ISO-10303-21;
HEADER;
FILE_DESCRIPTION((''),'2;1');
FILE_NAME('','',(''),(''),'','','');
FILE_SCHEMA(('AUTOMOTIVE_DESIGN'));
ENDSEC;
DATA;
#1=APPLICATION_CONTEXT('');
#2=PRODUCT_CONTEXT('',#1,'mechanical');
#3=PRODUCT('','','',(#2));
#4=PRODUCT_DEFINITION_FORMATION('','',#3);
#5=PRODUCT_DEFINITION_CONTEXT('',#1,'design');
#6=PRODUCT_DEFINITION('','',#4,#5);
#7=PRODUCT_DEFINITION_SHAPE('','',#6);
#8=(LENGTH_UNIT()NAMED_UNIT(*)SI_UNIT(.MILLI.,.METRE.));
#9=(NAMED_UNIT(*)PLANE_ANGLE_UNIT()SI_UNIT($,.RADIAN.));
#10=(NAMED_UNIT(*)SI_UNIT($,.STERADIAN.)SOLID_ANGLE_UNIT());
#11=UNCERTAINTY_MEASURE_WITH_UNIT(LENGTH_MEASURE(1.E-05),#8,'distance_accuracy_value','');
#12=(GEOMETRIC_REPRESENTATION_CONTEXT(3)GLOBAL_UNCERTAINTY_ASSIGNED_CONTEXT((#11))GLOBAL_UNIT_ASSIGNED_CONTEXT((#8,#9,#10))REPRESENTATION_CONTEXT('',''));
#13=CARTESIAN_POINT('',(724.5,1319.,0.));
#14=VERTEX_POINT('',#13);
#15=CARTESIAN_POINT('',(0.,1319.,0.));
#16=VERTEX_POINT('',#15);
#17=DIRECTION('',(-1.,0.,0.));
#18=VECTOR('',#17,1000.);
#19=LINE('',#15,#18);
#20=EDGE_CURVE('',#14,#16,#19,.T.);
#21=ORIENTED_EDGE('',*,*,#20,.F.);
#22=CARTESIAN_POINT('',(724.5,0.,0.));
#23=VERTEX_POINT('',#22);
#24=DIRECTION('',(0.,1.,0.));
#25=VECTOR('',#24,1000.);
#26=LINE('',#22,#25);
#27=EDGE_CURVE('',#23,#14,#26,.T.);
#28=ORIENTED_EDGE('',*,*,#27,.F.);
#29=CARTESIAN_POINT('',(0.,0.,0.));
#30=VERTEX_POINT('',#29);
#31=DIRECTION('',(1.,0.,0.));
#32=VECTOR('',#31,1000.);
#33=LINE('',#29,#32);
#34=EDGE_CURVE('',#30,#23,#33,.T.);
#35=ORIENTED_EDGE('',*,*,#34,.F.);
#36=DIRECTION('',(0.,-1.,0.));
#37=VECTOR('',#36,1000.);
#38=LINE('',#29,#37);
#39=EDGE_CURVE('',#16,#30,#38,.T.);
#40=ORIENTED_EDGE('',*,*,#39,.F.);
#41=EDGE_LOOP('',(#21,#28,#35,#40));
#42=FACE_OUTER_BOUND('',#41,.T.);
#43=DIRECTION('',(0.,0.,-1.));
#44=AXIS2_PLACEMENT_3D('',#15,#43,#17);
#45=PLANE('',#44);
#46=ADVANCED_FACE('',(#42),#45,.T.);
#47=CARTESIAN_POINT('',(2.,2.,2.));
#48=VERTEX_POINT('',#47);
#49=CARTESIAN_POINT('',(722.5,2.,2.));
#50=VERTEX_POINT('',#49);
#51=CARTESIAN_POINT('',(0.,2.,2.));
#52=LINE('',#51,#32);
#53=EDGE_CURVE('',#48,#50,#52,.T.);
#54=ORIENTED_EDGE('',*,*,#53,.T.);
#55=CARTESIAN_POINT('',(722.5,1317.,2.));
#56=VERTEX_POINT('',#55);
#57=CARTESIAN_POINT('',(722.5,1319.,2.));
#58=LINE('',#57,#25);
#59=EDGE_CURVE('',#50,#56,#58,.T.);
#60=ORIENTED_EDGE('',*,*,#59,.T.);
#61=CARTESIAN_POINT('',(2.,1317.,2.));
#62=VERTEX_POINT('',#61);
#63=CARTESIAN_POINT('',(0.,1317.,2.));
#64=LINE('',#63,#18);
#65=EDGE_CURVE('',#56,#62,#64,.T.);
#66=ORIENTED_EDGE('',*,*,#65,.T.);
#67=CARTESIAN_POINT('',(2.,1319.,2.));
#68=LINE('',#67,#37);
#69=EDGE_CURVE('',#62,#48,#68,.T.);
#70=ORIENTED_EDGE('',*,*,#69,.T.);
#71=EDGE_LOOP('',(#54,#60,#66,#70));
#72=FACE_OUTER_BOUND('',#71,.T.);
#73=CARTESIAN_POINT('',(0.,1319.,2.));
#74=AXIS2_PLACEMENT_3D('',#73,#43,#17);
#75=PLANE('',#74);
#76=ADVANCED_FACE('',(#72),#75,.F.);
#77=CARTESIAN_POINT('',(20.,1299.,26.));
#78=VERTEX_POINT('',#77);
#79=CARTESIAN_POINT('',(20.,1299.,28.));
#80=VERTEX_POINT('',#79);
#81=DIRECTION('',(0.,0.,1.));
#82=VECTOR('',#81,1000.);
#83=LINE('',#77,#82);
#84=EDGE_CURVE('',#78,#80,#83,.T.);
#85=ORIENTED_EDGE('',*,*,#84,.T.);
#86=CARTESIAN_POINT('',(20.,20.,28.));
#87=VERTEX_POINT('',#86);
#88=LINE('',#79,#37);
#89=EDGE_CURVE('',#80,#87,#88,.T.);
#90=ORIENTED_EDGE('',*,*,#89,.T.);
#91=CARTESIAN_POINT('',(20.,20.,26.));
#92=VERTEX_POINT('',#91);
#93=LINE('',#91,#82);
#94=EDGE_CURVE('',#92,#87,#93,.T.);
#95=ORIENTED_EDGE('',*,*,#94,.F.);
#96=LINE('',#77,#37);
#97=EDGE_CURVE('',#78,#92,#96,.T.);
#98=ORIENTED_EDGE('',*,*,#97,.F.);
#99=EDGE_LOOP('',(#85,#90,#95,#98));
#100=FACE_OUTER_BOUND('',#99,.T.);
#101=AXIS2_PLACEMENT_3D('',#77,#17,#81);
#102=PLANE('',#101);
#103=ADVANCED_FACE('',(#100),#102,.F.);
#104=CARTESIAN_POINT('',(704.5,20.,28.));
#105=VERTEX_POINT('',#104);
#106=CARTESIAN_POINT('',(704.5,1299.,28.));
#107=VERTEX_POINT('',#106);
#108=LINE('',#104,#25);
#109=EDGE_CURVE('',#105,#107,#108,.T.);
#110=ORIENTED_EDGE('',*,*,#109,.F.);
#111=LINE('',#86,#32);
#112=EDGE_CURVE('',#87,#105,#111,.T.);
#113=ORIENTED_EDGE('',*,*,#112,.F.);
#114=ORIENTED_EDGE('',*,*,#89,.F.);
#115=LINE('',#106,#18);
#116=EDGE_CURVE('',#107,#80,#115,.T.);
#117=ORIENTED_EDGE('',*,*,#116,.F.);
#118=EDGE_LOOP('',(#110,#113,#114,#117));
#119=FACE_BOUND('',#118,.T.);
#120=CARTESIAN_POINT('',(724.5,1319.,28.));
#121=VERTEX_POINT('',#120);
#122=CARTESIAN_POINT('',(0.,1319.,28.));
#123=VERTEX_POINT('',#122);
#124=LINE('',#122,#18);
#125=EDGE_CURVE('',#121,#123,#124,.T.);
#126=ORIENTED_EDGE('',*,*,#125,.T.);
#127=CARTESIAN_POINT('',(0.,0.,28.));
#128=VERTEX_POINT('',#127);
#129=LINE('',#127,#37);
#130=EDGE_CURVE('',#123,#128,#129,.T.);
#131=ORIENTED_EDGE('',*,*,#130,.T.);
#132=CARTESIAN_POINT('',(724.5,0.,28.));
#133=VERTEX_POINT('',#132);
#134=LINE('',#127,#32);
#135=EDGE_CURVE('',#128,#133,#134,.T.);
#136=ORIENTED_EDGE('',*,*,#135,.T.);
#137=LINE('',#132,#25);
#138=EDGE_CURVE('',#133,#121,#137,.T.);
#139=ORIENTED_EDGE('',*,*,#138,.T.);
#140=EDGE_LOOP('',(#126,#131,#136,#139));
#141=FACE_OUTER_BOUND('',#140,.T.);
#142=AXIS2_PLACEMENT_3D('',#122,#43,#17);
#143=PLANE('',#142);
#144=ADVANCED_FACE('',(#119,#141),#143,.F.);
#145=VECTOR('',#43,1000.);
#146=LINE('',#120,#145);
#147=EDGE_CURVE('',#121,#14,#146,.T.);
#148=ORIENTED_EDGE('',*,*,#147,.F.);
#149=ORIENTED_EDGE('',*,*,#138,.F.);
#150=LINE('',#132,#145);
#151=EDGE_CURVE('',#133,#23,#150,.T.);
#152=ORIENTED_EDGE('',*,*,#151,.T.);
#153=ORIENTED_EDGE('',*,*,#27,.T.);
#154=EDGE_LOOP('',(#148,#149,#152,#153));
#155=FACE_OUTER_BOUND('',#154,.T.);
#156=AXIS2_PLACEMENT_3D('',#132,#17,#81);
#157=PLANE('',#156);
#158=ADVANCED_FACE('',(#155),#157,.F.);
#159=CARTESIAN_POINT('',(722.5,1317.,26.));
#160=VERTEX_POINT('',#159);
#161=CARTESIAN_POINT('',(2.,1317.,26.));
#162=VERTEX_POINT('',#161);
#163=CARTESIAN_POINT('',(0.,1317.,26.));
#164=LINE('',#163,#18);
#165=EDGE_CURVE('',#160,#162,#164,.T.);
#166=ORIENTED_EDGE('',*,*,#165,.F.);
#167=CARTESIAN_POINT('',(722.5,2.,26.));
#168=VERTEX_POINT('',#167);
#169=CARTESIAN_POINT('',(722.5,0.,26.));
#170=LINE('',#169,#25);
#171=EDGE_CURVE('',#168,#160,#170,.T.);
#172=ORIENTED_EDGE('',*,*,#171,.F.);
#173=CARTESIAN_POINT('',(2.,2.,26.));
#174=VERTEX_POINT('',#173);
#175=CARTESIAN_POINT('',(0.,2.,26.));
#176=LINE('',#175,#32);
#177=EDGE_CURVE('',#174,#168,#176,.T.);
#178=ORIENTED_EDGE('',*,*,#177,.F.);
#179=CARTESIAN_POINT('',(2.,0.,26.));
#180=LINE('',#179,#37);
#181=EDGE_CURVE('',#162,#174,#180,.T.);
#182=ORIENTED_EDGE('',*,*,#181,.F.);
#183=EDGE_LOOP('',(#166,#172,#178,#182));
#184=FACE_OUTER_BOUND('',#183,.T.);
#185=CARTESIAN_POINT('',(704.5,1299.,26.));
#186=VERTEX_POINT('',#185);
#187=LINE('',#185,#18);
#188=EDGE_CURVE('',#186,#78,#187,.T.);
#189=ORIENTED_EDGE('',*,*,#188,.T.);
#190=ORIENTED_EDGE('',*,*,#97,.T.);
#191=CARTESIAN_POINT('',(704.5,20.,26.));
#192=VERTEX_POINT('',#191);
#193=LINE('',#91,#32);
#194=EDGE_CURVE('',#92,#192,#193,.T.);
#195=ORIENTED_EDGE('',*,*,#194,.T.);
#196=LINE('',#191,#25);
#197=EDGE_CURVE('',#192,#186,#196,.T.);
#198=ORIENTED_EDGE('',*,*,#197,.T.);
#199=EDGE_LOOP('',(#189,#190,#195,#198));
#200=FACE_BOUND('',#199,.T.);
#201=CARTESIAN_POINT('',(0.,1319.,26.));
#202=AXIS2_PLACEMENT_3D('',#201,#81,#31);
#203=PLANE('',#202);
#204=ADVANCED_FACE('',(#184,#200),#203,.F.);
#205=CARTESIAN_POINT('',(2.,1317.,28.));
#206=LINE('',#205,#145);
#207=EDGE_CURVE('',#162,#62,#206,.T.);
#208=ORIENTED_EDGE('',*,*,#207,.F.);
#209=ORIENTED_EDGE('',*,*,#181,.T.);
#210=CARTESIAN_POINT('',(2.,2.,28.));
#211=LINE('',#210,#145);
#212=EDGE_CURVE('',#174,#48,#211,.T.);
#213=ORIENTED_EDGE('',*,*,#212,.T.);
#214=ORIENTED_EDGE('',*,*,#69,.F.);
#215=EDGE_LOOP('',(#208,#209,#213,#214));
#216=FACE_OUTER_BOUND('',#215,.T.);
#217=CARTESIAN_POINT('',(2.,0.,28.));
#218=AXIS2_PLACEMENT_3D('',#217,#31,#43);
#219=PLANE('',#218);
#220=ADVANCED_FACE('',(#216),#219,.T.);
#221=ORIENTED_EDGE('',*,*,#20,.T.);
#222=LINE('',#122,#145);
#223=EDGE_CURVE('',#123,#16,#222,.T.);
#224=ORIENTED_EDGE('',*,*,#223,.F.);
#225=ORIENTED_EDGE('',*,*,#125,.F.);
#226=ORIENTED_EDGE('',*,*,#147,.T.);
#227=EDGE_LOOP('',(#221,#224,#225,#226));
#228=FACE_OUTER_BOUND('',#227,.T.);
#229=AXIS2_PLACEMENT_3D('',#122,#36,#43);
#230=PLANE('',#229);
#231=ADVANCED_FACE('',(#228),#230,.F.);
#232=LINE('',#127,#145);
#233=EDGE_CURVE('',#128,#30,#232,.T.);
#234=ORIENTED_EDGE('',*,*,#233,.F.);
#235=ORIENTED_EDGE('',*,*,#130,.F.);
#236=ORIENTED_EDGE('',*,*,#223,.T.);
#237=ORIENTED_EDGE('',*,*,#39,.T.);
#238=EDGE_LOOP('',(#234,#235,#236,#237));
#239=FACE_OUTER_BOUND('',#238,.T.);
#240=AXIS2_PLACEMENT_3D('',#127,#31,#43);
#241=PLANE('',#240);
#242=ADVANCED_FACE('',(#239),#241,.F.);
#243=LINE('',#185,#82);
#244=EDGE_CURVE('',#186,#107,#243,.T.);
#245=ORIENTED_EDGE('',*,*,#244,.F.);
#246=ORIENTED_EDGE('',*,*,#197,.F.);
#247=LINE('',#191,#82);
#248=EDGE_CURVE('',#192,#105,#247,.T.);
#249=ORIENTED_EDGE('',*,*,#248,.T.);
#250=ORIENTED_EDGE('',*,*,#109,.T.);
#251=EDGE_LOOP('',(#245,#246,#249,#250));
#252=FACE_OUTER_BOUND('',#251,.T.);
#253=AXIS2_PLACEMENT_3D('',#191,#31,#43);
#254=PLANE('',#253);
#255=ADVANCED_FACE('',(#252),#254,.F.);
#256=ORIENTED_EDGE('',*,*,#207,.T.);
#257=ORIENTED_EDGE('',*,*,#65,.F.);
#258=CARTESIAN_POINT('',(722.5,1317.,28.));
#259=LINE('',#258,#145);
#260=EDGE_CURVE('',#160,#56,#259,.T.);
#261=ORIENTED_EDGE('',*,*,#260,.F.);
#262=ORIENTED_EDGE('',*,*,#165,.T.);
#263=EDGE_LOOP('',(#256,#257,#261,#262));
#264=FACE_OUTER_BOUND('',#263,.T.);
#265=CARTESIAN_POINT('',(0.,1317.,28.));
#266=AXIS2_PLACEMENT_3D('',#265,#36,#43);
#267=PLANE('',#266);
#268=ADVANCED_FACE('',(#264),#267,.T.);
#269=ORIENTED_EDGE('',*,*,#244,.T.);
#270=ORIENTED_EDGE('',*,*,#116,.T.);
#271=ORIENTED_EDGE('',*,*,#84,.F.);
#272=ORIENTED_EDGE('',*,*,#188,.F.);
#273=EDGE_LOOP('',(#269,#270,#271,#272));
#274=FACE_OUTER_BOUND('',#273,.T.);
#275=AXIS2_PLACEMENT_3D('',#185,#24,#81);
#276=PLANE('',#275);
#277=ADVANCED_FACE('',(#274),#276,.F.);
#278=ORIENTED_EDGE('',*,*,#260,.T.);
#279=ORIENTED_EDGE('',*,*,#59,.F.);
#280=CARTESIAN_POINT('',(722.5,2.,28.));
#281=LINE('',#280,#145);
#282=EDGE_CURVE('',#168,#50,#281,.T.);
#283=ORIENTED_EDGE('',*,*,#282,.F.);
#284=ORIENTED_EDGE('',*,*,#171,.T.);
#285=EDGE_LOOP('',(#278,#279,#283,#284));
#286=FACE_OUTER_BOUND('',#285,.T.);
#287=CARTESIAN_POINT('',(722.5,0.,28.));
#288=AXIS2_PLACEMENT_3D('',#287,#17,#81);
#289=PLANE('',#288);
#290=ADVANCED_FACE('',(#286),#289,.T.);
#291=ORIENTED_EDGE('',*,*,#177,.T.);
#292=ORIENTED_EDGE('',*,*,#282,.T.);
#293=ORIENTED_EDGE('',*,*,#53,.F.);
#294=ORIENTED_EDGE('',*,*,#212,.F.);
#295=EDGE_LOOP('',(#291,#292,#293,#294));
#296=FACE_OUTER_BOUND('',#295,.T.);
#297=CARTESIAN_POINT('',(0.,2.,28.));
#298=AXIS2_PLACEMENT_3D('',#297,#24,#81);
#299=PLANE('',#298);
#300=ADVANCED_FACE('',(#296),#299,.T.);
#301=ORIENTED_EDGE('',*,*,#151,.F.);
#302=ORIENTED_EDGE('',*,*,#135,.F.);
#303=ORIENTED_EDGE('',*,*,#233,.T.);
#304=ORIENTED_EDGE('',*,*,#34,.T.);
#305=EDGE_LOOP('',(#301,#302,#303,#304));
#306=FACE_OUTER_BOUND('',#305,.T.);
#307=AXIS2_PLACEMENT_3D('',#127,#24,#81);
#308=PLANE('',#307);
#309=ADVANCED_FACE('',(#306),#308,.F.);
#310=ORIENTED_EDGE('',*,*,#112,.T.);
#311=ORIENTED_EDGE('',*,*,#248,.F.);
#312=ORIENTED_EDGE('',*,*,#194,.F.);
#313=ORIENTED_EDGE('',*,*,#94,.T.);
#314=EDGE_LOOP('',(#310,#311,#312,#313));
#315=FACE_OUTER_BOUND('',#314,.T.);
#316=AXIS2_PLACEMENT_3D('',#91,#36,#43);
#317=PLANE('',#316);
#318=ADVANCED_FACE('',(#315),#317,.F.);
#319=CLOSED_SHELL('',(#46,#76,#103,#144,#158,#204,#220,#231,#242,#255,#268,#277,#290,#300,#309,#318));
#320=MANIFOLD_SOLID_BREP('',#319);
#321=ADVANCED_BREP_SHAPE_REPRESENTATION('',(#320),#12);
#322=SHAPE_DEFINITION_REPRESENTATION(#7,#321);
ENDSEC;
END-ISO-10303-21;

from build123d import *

# Parameters (mm, degrees)
SKETCH_1_W      = 724.5
SKETCH_1_H      = 1319
EXTRUDE_1_DEPTH = 28
SHELL_1_T       = -2
SKETCH_2_W      = 724.5
SKETCH_2_H      = 1319
SKETCH_2_W_2    = 684.5
SKETCH_2_H_2    = 1279
EXTRUDE_2_DEPTH = 2


with BuildPart() as part:
    # 草图1 → 凸台-拉伸1 (new body)
    with BuildSketch(Plane.XY):
        with Locations((362.25, 659.5)):
            Rectangle(SKETCH_1_W, SKETCH_1_H)
    extrude(amount=EXTRUDE_1_DEPTH)

    # 抽壳1
    shell_1_openings = [part.faces().sort_by_distance(p)[0] for p in [
        (362.25, 659.5, 28),
    ]]
    offset(amount=SHELL_1_T, openings=shell_1_openings, kind=Kind.INTERSECTION)

    # 草图2 → 凸台-拉伸2 (add)
    with BuildSketch(Plane.XY.offset(28)):
        with Locations((362.25, 659.5)):
            Rectangle(SKETCH_2_W, SKETCH_2_H)
        with Locations((362.25, 659.5)):
            Rectangle(SKETCH_2_W_2, SKETCH_2_H_2, mode=Mode.SUBTRACT)
    extrude(amount=-EXTRUDE_2_DEPTH)


solid = part.part
